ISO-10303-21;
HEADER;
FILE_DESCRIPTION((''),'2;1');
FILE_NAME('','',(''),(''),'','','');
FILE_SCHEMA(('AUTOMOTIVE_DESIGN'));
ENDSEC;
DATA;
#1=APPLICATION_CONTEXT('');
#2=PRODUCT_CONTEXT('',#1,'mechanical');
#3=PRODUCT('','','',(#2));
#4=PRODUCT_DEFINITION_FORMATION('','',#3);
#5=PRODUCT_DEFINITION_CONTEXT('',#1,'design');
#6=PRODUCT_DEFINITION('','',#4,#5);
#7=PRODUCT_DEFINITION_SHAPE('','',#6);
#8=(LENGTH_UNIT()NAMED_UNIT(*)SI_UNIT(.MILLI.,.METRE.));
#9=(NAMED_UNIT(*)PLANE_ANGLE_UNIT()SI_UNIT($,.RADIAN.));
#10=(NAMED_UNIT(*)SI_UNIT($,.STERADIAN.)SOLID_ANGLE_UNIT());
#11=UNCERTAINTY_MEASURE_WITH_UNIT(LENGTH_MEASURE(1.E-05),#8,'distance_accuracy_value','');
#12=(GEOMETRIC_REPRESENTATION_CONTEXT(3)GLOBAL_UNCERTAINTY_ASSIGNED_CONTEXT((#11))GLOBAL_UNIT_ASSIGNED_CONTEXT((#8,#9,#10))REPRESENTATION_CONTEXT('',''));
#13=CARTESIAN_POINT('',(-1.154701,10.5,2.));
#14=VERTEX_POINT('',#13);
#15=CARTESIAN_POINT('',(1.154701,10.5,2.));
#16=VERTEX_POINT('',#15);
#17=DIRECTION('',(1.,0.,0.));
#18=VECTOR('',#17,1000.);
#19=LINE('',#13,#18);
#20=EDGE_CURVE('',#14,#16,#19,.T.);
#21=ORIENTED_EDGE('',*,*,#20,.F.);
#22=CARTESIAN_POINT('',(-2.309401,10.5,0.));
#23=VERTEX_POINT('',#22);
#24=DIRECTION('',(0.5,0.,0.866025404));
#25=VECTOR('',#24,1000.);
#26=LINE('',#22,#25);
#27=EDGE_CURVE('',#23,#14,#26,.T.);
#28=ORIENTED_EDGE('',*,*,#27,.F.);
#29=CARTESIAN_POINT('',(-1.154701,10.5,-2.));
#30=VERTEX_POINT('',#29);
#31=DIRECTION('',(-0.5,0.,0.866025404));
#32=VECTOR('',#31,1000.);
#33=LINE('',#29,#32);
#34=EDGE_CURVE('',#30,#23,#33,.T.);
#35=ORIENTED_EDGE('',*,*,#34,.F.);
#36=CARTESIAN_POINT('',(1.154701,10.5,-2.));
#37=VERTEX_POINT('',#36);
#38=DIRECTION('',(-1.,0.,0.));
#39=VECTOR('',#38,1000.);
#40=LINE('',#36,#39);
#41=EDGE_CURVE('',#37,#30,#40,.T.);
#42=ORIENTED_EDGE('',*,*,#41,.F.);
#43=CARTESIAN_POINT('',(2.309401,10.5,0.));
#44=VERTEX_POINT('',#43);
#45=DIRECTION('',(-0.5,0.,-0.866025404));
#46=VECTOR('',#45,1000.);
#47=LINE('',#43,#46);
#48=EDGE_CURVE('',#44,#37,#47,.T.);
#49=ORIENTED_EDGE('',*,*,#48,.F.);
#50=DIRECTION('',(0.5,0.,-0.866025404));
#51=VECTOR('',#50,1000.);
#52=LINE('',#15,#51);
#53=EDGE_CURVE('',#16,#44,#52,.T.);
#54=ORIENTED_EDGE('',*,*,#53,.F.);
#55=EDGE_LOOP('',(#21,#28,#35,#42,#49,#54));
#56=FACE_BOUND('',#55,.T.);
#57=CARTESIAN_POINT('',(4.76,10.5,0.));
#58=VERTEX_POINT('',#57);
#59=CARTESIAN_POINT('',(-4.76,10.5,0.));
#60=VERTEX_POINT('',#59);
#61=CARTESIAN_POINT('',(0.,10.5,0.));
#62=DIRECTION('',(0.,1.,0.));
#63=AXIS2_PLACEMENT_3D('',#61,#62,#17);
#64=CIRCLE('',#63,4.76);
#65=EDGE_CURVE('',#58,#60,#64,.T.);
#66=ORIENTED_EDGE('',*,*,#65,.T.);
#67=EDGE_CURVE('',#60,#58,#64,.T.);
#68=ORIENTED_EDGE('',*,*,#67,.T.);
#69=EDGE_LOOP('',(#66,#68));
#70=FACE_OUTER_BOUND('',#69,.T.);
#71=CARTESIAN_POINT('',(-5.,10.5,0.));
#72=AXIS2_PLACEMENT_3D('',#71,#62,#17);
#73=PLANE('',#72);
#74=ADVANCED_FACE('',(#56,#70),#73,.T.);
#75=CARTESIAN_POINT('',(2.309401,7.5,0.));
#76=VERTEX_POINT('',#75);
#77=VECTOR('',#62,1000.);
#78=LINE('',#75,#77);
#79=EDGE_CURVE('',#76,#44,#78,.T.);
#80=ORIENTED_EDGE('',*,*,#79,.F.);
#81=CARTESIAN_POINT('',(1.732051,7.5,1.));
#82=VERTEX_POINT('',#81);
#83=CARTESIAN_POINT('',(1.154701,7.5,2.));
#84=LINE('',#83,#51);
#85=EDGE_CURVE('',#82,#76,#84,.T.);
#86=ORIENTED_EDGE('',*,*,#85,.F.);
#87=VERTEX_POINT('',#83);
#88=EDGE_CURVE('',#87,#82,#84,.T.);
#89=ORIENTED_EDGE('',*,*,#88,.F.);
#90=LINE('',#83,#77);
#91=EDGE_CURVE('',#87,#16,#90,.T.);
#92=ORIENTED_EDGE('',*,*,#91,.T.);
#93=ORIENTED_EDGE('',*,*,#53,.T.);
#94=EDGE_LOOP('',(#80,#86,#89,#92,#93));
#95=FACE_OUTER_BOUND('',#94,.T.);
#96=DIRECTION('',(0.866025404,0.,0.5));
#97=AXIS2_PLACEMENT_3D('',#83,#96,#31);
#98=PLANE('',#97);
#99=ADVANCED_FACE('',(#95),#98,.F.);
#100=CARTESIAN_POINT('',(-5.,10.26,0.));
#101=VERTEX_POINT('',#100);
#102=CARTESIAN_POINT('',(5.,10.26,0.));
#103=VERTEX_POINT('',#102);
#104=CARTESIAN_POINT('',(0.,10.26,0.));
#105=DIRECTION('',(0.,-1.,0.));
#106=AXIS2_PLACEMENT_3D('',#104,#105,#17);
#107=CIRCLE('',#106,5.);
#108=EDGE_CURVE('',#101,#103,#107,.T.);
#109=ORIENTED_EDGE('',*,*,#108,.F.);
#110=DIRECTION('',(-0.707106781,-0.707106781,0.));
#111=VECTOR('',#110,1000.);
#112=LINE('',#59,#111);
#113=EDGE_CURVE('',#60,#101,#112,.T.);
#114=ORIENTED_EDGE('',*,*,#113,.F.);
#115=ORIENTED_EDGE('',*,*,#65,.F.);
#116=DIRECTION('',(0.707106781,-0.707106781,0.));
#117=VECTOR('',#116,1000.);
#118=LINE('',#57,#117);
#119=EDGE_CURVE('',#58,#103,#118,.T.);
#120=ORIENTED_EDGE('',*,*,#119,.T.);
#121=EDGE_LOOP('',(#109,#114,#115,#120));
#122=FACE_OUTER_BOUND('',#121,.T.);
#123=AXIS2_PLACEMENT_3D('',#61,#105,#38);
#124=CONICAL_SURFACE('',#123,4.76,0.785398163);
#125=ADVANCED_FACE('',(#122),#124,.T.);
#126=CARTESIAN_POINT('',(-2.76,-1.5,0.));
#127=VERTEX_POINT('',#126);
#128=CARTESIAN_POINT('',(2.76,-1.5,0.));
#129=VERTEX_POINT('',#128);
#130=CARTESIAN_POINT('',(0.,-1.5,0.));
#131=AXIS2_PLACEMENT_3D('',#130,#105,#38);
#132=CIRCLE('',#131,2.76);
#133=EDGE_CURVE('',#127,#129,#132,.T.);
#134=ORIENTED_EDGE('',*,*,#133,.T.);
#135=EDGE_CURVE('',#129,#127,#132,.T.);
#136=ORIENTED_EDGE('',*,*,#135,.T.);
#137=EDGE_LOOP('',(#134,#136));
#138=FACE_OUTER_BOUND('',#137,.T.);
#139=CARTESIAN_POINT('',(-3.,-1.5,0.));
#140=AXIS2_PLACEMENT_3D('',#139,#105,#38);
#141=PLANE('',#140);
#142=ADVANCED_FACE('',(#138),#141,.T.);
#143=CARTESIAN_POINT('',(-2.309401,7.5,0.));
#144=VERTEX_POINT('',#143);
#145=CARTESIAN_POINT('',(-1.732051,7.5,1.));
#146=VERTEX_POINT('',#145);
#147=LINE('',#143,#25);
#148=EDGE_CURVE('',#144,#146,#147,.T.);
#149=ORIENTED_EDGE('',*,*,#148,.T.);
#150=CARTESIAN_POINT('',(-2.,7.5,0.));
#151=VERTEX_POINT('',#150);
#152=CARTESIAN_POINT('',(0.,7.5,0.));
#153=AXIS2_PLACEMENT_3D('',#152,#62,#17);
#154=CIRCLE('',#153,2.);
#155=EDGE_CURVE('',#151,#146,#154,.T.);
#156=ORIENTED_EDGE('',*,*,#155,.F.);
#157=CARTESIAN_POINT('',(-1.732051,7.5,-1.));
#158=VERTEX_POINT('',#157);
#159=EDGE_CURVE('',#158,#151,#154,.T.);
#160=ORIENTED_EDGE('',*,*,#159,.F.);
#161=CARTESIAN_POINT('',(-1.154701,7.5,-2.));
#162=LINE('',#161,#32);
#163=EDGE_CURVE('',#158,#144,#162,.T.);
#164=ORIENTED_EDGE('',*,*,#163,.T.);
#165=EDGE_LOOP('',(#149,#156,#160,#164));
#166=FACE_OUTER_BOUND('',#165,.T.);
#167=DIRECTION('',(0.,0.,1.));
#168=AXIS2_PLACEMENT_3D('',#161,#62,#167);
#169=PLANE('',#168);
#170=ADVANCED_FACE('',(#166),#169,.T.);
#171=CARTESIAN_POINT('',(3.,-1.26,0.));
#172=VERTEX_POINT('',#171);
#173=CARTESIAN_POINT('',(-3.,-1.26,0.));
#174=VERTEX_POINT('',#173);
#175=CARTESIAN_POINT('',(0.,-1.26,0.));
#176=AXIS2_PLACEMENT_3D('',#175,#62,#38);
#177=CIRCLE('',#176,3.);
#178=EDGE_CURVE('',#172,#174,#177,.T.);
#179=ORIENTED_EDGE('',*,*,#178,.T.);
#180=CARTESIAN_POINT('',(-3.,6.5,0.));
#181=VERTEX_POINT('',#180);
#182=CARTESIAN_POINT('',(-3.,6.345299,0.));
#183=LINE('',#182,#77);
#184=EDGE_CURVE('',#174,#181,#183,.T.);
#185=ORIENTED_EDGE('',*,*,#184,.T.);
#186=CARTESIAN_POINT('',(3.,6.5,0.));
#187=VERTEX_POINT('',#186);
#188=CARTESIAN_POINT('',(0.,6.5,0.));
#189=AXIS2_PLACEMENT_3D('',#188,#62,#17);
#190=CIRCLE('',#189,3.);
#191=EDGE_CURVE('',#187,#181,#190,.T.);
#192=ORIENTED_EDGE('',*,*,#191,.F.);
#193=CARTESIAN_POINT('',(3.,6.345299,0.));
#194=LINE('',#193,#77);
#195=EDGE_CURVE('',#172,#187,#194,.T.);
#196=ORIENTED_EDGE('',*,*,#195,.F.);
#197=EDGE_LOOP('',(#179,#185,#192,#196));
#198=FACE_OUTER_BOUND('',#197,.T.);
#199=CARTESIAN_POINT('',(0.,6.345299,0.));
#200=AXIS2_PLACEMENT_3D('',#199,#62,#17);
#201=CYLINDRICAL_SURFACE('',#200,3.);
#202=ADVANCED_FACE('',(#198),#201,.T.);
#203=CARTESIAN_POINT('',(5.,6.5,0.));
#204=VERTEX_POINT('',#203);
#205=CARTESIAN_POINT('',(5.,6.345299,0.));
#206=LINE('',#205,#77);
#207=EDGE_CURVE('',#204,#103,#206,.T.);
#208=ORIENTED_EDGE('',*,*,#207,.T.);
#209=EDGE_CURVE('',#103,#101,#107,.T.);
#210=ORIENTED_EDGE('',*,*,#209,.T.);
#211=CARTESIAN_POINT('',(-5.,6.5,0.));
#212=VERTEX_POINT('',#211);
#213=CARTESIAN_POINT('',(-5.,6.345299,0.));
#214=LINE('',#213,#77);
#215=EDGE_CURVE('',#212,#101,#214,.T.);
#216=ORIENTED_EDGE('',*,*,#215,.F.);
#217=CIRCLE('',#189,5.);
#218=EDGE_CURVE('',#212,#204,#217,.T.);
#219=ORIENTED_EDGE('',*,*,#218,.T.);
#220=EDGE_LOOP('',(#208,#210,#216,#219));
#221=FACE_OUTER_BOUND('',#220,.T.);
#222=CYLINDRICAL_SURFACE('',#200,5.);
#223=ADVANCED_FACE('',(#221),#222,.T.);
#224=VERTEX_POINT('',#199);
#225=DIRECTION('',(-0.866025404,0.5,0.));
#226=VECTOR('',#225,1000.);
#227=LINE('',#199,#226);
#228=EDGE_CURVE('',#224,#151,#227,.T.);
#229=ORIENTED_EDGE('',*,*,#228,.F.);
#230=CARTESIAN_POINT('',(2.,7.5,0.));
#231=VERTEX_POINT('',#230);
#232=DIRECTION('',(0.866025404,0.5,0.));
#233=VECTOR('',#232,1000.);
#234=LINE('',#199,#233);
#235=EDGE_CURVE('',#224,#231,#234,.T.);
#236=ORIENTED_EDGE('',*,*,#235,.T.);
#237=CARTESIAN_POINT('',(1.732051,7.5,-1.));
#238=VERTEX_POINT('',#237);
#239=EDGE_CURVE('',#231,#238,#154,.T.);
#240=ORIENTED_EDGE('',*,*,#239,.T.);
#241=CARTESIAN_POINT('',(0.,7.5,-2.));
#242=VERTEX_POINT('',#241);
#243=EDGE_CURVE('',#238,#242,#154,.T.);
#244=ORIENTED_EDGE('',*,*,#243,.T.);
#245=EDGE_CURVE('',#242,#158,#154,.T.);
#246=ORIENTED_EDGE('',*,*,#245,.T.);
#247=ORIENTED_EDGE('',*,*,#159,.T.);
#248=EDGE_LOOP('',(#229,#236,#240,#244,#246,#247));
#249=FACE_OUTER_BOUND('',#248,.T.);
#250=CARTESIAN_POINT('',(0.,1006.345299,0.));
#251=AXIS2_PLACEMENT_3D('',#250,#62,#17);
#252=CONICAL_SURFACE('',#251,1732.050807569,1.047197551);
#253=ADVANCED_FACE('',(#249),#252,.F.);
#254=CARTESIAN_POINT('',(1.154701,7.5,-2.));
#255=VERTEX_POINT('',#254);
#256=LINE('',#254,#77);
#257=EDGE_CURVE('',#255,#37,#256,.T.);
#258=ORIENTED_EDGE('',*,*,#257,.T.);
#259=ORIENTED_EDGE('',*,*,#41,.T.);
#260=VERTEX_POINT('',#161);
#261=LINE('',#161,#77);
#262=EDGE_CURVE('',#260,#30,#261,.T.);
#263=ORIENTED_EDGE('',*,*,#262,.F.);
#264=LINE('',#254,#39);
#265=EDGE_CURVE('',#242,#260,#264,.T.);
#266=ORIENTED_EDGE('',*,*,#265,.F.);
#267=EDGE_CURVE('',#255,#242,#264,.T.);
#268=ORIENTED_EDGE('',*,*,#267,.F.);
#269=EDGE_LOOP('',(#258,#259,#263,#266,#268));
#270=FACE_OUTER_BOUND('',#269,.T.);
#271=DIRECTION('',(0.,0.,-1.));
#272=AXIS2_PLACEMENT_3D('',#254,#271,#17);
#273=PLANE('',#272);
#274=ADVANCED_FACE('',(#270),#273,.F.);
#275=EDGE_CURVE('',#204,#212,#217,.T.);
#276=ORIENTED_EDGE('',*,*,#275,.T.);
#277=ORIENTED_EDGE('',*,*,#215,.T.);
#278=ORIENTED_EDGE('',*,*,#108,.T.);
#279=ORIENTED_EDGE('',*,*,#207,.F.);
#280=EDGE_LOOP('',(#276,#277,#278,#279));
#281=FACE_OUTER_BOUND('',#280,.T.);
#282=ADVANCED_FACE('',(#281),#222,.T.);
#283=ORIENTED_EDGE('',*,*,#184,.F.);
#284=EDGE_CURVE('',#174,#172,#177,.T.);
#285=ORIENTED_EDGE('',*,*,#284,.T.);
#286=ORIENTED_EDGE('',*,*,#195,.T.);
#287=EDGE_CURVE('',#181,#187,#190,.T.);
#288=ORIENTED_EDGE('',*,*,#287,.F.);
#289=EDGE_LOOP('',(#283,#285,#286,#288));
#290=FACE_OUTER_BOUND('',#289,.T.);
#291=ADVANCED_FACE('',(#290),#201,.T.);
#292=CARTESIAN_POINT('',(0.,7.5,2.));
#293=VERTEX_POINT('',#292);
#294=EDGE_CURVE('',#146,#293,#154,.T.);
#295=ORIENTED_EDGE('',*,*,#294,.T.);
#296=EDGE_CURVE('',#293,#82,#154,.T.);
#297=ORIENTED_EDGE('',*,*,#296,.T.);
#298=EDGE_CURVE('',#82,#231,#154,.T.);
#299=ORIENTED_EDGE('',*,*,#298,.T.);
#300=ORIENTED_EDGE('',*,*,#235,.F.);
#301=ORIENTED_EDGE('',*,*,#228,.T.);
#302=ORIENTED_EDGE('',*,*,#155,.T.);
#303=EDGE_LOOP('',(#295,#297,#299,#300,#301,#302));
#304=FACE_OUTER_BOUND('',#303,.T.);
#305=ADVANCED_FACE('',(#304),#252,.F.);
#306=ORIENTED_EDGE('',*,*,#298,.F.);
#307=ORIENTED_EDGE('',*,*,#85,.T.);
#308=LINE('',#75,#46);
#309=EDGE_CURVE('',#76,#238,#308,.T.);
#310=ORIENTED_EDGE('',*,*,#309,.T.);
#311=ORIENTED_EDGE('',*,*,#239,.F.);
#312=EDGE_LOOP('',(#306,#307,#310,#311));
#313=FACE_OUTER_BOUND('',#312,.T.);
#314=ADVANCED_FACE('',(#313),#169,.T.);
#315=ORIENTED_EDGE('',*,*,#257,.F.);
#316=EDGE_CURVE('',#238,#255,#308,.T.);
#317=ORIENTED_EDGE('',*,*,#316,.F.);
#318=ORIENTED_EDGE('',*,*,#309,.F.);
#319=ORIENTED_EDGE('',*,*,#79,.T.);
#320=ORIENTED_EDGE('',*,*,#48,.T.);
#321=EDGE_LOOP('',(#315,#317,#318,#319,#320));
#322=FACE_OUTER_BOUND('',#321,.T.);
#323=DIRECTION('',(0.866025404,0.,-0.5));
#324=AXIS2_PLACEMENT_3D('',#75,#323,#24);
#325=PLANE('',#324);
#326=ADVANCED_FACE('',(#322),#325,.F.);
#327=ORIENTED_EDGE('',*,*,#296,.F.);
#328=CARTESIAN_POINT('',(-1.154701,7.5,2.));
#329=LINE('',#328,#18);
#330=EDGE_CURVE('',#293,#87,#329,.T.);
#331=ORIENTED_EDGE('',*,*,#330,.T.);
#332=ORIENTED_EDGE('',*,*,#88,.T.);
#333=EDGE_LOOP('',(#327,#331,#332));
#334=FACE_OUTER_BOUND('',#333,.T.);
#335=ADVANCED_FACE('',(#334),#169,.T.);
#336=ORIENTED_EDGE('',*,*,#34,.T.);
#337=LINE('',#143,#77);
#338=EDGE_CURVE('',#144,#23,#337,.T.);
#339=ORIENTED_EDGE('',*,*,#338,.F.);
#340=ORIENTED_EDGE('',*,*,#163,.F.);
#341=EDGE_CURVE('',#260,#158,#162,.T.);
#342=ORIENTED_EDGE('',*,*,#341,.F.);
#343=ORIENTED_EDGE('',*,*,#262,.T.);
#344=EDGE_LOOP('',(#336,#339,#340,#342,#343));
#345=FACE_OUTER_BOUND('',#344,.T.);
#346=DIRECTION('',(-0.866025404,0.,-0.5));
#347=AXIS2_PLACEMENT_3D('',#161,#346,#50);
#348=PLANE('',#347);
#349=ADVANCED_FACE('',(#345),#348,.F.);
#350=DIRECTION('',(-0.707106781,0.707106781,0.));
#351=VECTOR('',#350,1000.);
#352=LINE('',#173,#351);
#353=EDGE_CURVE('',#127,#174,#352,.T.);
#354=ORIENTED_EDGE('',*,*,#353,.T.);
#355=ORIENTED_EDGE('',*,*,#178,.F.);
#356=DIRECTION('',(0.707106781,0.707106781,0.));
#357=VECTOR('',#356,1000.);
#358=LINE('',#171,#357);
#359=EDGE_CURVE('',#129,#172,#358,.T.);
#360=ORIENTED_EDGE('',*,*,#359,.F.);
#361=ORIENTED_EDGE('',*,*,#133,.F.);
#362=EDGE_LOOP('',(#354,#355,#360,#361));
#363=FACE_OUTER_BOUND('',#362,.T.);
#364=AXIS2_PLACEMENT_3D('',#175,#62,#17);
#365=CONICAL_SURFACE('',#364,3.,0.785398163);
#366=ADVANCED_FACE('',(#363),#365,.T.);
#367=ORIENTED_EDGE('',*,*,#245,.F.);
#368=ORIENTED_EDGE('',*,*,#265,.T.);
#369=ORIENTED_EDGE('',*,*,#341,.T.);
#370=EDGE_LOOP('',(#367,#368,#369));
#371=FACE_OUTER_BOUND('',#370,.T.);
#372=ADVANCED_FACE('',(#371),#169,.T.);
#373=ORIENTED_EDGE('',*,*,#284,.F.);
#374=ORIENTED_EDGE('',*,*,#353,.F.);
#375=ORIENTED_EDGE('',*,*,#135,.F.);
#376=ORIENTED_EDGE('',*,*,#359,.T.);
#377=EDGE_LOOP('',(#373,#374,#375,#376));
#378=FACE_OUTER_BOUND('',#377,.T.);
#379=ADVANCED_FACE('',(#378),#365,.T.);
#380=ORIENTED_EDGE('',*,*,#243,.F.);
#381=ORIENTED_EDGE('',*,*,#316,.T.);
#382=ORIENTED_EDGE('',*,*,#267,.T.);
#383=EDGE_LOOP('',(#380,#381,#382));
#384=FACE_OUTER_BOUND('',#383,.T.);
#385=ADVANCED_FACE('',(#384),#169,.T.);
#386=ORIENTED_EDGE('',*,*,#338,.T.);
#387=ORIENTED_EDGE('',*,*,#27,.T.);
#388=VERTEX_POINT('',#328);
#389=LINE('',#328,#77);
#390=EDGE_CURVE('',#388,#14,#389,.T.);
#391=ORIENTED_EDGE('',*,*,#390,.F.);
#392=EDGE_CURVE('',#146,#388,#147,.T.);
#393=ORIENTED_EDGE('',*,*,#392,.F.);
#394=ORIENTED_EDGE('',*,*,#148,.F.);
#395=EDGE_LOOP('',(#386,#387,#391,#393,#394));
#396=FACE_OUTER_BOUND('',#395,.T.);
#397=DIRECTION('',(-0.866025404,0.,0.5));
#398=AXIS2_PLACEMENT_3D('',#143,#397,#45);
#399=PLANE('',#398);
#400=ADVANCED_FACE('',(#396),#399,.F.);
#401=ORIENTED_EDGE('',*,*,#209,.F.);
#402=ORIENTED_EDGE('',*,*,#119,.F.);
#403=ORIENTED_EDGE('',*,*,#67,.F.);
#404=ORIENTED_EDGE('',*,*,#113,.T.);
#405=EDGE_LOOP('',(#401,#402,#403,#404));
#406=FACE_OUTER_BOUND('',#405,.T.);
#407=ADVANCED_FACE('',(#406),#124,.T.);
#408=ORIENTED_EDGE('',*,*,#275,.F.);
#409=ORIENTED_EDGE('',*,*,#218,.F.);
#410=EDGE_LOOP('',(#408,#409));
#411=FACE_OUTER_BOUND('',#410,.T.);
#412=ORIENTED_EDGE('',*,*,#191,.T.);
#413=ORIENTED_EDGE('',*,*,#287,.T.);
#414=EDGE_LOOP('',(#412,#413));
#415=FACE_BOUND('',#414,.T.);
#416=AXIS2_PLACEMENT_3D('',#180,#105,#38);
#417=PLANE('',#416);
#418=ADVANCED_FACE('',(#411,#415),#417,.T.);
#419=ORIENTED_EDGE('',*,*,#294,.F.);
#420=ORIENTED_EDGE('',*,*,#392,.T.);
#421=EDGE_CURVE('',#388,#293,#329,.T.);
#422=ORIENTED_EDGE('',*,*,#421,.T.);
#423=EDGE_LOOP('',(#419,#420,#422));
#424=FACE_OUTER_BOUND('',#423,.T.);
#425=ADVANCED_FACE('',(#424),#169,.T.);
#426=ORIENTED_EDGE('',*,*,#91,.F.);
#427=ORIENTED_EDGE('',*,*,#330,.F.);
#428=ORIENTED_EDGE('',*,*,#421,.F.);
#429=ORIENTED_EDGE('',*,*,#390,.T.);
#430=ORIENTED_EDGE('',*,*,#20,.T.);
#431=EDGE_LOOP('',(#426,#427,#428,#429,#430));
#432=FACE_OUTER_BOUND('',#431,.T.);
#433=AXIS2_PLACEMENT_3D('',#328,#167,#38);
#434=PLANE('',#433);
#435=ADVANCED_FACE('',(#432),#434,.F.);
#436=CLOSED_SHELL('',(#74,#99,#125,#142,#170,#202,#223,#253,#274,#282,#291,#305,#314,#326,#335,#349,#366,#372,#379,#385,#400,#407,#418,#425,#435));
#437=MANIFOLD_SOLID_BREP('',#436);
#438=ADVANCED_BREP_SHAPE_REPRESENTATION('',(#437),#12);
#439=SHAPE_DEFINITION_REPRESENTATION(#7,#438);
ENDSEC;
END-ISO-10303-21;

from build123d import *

# Parameters (mm, degrees)
CHAMFER1_SIZE         = 0.24
CUT_EXTRUDE1_DEPTH    = 3
BODY_MOVE_COPY1_ANGLE = 180


with BuildPart() as part:
    # Sketch2 → Revolve1 (revolve)
    with BuildSketch(Plane.XY):
        Polygon((2, -4), (2, -1), (0, 0.154700538), (0, 8), (3, 8), (3, 0), (5, 0), (5, -4), align=None)
    revolve(axis=Axis((0, 0.154700538, 0), (0, 1, 0)))

    # Chamfer1
    chamfer1_edges = [part.edges().sort_by_distance(p)[0] for p in [
        (-5, -4, 0),
        (-3, 8, 0),
    ]]
    chamfer(chamfer1_edges, length=CHAMFER1_SIZE)

    # Sketch3 → Cut-Extrude1 (cut)
    with BuildSketch(Plane.XZ.offset(4)):
        Polygon((-1.154700538, 2), (-2.309401077, 0), (-1.154700538, -2), (1.154700538, -2), (2.309401077, 0), (1.154700538, 2), align=None)
    extrude(amount=-CUT_EXTRUDE1_DEPTH, mode=Mode.SUBTRACT)


with BuildPart() as part_1:
    # Body-Move/Copy1: moved
    add(part.part.rotate(Axis((0, 3.25, 0), (1, 0, 0)), BODY_MOVE_COPY1_ANGLE))


solid = part_1.part
